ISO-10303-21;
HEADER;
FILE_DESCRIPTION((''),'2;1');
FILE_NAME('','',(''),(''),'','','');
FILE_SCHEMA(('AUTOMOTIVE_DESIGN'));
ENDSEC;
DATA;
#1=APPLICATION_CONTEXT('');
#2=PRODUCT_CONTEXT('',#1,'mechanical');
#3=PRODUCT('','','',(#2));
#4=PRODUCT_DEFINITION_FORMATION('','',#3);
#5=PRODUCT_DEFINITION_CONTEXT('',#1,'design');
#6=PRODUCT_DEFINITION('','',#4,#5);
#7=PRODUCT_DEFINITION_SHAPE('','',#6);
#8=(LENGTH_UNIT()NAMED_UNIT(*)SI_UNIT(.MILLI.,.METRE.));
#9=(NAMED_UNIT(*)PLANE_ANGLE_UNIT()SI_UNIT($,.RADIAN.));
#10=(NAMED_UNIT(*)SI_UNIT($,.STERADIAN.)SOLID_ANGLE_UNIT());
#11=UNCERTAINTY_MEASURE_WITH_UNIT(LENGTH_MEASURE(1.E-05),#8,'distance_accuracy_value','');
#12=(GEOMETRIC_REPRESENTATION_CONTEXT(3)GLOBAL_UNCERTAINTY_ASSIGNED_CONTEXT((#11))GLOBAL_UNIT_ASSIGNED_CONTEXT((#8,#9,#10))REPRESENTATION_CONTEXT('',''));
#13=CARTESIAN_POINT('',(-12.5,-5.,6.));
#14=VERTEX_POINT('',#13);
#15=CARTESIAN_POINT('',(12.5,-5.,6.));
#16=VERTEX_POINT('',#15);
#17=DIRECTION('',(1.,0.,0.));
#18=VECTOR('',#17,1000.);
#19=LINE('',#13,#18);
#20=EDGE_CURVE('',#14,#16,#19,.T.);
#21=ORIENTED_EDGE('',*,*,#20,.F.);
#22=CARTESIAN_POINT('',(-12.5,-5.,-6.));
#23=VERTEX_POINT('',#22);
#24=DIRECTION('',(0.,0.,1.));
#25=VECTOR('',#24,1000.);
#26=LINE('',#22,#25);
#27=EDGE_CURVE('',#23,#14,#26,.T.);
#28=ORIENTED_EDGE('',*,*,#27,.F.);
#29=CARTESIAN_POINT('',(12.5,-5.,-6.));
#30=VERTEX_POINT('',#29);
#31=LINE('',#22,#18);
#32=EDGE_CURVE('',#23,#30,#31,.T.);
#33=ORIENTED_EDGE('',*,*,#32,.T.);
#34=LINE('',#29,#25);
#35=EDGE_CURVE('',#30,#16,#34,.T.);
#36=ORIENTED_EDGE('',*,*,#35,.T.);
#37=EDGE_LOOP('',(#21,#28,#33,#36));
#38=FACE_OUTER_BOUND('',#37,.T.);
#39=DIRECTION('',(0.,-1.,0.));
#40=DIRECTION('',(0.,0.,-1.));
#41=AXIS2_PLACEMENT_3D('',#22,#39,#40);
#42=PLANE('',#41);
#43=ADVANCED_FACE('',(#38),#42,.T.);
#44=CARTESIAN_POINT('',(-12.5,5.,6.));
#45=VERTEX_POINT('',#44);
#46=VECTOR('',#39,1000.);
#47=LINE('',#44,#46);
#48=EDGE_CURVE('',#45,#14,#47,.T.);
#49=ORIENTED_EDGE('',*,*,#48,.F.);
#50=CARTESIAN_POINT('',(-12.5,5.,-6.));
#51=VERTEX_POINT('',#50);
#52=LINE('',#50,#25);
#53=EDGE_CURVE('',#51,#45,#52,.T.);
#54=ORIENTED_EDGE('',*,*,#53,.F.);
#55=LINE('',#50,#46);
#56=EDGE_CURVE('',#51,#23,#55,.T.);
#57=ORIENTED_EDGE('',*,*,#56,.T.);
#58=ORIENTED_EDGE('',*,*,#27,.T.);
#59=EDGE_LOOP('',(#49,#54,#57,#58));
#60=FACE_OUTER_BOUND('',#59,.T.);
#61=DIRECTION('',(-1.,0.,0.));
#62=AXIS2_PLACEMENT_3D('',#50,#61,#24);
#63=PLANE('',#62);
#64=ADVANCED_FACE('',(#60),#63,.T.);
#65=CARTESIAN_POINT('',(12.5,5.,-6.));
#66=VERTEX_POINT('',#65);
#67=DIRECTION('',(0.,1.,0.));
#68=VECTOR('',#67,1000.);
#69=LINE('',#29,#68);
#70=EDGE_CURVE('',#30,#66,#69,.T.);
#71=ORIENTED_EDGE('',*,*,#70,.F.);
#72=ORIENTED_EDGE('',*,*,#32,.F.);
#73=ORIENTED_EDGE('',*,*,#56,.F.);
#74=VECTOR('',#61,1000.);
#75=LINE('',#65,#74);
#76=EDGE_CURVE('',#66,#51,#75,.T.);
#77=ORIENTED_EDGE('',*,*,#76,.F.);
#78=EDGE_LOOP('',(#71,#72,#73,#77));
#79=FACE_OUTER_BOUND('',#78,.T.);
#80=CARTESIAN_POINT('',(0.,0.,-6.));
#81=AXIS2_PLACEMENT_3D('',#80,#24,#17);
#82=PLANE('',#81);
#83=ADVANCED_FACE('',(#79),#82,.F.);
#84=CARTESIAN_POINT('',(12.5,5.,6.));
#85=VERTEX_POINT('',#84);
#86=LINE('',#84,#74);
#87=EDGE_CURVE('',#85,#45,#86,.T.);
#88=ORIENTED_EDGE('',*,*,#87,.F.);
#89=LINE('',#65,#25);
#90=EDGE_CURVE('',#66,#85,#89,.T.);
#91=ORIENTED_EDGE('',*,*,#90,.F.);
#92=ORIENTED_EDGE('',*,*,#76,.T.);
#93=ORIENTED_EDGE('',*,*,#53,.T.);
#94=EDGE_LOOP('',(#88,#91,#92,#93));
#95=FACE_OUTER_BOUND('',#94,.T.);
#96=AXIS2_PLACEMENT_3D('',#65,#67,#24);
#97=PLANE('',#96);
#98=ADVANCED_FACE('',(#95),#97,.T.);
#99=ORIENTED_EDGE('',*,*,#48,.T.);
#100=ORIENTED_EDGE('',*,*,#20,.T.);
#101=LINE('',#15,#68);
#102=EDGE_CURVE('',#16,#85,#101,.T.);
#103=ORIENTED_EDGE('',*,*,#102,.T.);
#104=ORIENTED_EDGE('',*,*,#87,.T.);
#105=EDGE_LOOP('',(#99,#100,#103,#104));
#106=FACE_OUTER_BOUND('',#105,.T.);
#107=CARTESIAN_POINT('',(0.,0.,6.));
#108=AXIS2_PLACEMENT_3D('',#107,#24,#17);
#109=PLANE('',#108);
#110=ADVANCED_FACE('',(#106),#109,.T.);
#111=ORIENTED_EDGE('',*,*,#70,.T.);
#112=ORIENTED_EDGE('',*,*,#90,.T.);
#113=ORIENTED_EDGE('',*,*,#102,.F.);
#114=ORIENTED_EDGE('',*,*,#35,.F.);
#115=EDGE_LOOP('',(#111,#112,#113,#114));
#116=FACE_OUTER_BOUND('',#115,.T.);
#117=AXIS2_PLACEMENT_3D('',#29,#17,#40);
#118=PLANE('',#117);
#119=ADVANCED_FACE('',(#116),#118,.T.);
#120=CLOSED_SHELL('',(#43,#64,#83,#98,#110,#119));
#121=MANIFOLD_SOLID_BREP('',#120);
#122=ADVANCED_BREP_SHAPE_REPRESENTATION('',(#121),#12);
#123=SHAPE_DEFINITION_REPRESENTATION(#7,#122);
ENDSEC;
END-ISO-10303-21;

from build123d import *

# Parameters (mm, degrees)
SKETCH_1_W      = 25
SKETCH_1_H      = 10
EXTRUDE_1_DEPTH = 6


with BuildPart() as part:
    # 草图1 → 凸台-拉伸1 (new, symmetric)
    with BuildSketch(Plane.XY):
        Rectangle(SKETCH_1_W, SKETCH_1_H)
    extrude(amount=EXTRUDE_1_DEPTH, both=True)


solid = part.part
